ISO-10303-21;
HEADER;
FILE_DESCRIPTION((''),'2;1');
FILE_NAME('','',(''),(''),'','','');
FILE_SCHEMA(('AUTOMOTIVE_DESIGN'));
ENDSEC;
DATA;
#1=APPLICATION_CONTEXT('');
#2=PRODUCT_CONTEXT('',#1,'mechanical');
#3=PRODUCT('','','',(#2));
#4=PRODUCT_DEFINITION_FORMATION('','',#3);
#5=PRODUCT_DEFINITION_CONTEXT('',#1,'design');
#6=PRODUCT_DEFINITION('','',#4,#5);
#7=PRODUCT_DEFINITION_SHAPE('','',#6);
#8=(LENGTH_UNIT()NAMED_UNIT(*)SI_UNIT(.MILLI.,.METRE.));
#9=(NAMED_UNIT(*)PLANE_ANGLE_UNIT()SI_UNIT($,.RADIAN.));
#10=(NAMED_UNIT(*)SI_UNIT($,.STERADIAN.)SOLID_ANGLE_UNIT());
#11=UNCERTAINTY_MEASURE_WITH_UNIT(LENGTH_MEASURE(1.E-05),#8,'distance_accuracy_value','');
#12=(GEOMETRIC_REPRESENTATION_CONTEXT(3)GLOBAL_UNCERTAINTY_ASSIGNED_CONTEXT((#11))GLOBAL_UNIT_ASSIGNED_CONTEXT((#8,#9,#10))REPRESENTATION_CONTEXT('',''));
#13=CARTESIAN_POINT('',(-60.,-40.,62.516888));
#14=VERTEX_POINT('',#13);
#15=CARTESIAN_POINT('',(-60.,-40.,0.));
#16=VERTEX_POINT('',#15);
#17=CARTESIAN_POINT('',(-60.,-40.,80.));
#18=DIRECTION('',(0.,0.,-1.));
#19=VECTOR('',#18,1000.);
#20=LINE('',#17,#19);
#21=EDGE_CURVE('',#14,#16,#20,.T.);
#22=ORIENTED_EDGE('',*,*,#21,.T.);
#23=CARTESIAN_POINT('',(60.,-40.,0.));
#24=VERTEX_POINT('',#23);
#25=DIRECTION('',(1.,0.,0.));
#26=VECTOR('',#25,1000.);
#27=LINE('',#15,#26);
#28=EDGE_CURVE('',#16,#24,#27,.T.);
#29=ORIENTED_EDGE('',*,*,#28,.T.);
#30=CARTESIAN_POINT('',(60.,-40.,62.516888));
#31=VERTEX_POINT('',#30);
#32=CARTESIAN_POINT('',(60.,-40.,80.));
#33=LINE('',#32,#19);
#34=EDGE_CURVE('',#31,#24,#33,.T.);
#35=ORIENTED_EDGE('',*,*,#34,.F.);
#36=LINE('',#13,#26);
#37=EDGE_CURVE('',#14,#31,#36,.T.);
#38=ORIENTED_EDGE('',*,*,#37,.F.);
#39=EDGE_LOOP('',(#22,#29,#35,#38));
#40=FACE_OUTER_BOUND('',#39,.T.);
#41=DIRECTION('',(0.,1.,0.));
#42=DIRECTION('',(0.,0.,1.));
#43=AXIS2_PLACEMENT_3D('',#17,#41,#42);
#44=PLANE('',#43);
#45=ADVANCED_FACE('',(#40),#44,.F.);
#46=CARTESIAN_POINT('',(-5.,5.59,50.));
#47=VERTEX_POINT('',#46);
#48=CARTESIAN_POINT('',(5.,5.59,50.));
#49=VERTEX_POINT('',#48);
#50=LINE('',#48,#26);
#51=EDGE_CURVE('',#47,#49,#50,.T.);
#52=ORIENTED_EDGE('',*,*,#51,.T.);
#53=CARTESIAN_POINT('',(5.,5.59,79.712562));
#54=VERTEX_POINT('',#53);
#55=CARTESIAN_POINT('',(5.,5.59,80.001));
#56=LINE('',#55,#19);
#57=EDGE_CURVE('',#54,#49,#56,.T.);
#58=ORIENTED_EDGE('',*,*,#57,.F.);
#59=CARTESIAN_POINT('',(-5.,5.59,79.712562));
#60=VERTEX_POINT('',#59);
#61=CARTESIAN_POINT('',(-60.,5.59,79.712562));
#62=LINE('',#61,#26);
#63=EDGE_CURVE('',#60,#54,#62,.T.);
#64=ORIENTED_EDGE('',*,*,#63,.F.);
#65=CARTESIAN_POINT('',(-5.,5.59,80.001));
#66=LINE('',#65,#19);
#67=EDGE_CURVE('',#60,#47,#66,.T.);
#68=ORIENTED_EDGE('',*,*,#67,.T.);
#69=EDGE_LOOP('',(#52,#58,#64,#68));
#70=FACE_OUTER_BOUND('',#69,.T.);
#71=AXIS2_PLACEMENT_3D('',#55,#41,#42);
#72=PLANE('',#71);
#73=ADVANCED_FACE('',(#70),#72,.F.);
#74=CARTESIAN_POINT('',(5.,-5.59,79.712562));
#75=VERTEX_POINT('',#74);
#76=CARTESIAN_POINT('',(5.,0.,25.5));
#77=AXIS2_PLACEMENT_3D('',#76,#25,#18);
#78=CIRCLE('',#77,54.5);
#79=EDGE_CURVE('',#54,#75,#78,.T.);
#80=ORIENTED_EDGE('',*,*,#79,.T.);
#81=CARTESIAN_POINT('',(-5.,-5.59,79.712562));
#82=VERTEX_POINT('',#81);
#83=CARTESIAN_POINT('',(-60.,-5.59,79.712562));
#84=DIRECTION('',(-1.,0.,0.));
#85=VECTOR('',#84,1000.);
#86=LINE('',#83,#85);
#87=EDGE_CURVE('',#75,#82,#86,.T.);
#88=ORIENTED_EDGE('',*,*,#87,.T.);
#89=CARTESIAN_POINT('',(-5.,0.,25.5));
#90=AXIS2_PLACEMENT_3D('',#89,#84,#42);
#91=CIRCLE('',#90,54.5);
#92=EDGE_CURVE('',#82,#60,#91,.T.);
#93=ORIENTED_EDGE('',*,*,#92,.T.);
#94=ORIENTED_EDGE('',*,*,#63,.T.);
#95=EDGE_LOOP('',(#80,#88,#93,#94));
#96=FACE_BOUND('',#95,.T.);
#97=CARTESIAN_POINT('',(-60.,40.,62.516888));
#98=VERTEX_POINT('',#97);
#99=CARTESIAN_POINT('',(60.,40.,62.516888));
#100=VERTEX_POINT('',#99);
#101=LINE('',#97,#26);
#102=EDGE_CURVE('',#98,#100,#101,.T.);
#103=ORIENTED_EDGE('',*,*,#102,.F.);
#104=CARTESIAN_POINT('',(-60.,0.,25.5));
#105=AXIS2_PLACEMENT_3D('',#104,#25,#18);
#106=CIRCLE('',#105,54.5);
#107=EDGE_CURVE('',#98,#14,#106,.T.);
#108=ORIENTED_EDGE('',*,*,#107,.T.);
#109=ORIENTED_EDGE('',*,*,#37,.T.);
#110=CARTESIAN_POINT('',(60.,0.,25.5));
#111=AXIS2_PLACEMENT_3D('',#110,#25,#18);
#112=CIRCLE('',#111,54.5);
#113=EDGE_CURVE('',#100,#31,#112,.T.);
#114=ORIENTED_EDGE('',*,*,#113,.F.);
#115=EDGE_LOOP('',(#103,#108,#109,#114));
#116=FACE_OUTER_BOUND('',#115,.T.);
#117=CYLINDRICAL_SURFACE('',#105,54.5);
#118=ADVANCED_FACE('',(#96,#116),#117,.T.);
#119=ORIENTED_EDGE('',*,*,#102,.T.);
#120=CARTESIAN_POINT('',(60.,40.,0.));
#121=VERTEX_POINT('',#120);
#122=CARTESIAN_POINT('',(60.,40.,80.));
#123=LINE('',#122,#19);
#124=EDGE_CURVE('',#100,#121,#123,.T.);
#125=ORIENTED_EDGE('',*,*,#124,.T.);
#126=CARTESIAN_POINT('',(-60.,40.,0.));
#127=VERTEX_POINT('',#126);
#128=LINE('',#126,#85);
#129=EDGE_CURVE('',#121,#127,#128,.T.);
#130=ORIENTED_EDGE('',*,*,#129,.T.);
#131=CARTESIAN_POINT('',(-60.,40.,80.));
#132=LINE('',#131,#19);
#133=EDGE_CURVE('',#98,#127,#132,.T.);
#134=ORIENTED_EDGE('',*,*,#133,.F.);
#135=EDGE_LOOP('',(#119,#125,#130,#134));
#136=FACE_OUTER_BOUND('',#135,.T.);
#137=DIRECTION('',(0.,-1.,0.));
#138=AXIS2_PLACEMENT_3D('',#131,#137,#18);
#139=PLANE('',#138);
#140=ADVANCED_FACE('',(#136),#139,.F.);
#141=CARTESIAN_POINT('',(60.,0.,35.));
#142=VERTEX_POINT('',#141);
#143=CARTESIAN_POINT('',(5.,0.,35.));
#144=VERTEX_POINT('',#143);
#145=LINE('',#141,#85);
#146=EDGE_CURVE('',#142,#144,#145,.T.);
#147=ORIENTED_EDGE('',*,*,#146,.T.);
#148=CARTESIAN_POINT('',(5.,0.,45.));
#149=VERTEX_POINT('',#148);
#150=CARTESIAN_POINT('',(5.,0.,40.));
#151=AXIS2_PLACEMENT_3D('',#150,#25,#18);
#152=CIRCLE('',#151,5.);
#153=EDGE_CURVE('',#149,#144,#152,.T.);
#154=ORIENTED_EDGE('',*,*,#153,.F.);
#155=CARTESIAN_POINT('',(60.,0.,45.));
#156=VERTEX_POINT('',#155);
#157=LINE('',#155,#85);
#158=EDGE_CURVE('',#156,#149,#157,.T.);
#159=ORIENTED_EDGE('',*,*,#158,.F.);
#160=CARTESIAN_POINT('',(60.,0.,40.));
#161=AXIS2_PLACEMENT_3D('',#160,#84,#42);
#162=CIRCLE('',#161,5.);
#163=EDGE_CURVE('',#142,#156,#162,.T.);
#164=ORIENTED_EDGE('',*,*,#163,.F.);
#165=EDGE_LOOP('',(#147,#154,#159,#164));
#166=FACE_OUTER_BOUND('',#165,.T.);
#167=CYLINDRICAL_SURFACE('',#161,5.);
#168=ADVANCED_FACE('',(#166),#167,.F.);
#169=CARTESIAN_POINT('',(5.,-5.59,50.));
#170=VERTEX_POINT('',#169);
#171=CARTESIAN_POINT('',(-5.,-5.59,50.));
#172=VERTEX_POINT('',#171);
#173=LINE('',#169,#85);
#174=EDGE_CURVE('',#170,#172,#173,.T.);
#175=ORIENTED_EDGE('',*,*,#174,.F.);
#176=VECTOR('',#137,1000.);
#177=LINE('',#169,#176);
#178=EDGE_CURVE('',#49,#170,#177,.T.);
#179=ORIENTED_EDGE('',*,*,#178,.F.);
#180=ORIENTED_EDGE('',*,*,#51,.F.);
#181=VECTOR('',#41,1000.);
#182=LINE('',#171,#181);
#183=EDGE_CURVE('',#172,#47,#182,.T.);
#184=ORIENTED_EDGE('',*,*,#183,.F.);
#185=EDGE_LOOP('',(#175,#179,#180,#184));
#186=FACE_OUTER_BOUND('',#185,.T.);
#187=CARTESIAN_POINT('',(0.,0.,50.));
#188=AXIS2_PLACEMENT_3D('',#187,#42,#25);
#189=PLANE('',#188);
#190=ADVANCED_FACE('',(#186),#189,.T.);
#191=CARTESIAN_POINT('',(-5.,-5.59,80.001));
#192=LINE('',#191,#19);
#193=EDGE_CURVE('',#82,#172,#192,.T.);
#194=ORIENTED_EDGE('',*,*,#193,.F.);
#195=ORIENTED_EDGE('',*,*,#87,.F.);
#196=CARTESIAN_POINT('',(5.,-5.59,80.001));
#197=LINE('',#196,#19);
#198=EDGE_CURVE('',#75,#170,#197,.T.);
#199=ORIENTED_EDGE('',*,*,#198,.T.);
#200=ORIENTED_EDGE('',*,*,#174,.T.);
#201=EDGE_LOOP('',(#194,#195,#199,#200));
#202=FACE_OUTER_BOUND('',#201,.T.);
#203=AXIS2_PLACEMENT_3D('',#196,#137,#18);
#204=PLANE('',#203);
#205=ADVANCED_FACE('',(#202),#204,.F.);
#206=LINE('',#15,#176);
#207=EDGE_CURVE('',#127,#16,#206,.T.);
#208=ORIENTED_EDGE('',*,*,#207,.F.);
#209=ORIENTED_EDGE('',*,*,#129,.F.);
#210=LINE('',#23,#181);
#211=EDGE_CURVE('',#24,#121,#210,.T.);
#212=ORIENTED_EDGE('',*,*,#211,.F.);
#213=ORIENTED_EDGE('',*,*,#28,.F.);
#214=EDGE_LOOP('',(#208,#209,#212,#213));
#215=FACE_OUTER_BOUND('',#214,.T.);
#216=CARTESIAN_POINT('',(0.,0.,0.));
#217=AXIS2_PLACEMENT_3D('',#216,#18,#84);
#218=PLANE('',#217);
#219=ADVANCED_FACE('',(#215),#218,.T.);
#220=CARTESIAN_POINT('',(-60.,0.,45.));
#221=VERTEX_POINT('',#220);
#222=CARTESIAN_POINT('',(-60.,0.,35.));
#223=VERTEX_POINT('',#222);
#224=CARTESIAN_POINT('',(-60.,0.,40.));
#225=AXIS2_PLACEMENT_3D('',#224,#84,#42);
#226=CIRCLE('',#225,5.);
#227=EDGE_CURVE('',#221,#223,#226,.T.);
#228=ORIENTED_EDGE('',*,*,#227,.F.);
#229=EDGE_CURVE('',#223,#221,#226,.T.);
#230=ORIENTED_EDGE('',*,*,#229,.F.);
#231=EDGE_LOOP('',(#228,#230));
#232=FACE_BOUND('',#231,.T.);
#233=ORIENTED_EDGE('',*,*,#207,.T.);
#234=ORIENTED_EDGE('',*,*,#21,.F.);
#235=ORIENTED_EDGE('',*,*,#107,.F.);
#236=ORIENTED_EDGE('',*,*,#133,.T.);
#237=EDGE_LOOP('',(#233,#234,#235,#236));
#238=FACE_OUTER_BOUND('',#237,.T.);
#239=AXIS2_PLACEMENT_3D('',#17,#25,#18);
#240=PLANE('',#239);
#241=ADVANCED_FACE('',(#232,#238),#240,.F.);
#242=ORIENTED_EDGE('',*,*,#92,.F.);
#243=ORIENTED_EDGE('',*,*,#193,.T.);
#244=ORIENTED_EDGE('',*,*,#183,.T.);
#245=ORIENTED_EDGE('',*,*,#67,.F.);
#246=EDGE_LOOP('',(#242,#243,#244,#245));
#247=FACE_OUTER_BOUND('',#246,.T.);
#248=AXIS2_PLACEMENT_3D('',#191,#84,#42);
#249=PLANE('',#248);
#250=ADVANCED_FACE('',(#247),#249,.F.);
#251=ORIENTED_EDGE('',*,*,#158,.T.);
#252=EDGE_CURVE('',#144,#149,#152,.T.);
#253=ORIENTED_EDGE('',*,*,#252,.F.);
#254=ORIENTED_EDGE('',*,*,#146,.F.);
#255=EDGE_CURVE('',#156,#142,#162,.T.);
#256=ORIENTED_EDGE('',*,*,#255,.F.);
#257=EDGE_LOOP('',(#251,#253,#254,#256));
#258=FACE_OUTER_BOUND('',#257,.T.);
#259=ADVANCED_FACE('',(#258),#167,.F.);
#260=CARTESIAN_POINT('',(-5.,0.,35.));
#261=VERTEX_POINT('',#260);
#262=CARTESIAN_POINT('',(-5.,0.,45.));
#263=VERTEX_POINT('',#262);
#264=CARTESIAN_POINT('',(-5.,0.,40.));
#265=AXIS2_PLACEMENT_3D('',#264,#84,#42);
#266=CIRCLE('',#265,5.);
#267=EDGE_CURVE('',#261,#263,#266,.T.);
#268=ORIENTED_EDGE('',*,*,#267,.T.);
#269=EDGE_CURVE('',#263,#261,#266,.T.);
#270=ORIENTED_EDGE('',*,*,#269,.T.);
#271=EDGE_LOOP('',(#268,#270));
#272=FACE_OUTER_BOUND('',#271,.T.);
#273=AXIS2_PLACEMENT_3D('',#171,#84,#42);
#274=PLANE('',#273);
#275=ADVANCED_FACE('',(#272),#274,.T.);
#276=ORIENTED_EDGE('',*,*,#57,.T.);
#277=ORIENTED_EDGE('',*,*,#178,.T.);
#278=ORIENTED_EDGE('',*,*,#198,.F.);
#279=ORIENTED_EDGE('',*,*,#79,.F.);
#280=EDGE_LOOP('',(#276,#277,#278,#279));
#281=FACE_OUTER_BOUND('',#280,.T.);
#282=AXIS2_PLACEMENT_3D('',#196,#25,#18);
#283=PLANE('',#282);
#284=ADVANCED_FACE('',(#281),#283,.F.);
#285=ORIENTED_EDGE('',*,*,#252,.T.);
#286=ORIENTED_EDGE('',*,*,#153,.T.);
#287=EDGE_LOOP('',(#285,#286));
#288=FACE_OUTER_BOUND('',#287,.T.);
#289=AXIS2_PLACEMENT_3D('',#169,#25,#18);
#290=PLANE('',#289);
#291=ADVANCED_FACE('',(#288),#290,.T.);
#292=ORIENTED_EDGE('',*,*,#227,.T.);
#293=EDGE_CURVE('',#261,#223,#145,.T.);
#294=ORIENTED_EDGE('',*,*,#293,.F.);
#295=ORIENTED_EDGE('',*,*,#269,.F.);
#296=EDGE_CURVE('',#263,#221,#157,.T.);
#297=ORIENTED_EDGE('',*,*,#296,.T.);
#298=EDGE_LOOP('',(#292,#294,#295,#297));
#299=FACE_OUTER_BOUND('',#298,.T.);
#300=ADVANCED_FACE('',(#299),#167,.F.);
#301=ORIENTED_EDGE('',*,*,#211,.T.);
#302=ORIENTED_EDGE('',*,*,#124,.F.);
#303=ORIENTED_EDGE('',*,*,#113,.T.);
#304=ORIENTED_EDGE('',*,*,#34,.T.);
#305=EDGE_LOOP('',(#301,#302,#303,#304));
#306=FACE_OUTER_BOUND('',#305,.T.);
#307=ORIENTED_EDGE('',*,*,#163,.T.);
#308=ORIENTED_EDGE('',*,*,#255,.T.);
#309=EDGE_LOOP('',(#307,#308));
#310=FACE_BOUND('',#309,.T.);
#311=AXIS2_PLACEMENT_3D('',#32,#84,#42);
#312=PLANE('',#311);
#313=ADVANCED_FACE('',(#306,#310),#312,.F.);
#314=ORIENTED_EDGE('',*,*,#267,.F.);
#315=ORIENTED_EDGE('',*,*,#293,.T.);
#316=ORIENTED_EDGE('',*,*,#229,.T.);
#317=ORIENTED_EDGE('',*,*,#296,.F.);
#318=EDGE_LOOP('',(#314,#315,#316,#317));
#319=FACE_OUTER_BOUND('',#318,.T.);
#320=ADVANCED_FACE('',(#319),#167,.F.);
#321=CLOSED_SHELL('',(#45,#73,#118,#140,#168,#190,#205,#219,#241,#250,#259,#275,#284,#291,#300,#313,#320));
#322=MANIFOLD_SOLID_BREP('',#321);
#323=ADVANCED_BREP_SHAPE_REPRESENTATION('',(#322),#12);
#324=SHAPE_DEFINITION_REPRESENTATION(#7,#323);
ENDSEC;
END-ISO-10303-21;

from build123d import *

# Parameters (mm, degrees)
SKETCH_1_W          = 120
SKETCH_1_H          = 80
EXTRUDE_1_DEPTH     = 80
SKETCH_2_R          = 5
CUT_EXTRUDE_1_DEPTH = 150.666295471
CUT_EXTRUDE_2_DEPTH = 150.666295471
CUT_EXTRUDE_3_REACH = 109.703
SKETCH_5_W          = 10
SKETCH_5_H          = 11.18
SKETCH_6_W          = 10
SKETCH_6_H          = 11.18
EXTRUDE_2_DEPTH     = 50


with BuildPart() as part:
    # 草图1 → 凸台-拉伸1 (new body)
    with BuildSketch(Plane.XY):
        Rectangle(SKETCH_1_W, SKETCH_1_H)
    extrude(amount=EXTRUDE_1_DEPTH)

    # 草图2 → 切除-拉伸1 (cut, through all)
    with BuildSketch(Plane.ZY.offset(60)):
        with Locations((40, 0)):
            Circle(SKETCH_2_R)
    extrude(amount=-CUT_EXTRUDE_1_DEPTH, mode=Mode.SUBTRACT)

    # 草图4 → 切除-拉伸2 (cut, through all)
    with BuildSketch(Plane(origin=(60, 0, 0), x_dir=(0, 0, -1), z_dir=(1, 0, 0))):
        with BuildLine():
            ThreePointArc((-80, 4.27e-07), (-75.438313853, 21.82692854), (-62.516888038, 40))
            Line((-62.516888038, 40), (-80, 40))
            Line((-80, 40), (-80, 4.27e-07))
        make_face()
        with BuildLine():
            ThreePointArc((-62.516888038, -40), (-75.438314024, -21.826928149), (-80, 4.27e-07))
            Line((-80, 4.27e-07), (-80, -40))
            Line((-80, -40), (-62.516888038, -40))
        make_face()
    extrude(amount=-CUT_EXTRUDE_2_DEPTH, mode=Mode.SUBTRACT)

    # 草图5 → 切除-拉伸3 (cut, up to next)
    with BuildSketch(Plane(origin=(0, 0, 0), x_dir=(-1, 0, 0), z_dir=(0, 0, -1)), mode=Mode.PRIVATE) as cut_extrude_3_sk1:
        Rectangle(SKETCH_5_W, SKETCH_5_H)
    cut_extrude_3_tool1 = extrude(cut_extrude_3_sk1.sketch, amount=-CUT_EXTRUDE_3_REACH, mode=Mode.PRIVATE) & part.part
    add(cut_extrude_3_tool1.solids().sort_by_distance((0, 0, 0))[0], mode=Mode.SUBTRACT)

    # 草图6 → 凸台-拉伸2 (add)
    with BuildSketch(Plane(origin=(0, 0, 0), x_dir=(-1, 0, 0), z_dir=(0, 0, -1))):
        Rectangle(SKETCH_6_W, SKETCH_6_H)
    extrude(amount=-EXTRUDE_2_DEPTH)


solid = part.part
